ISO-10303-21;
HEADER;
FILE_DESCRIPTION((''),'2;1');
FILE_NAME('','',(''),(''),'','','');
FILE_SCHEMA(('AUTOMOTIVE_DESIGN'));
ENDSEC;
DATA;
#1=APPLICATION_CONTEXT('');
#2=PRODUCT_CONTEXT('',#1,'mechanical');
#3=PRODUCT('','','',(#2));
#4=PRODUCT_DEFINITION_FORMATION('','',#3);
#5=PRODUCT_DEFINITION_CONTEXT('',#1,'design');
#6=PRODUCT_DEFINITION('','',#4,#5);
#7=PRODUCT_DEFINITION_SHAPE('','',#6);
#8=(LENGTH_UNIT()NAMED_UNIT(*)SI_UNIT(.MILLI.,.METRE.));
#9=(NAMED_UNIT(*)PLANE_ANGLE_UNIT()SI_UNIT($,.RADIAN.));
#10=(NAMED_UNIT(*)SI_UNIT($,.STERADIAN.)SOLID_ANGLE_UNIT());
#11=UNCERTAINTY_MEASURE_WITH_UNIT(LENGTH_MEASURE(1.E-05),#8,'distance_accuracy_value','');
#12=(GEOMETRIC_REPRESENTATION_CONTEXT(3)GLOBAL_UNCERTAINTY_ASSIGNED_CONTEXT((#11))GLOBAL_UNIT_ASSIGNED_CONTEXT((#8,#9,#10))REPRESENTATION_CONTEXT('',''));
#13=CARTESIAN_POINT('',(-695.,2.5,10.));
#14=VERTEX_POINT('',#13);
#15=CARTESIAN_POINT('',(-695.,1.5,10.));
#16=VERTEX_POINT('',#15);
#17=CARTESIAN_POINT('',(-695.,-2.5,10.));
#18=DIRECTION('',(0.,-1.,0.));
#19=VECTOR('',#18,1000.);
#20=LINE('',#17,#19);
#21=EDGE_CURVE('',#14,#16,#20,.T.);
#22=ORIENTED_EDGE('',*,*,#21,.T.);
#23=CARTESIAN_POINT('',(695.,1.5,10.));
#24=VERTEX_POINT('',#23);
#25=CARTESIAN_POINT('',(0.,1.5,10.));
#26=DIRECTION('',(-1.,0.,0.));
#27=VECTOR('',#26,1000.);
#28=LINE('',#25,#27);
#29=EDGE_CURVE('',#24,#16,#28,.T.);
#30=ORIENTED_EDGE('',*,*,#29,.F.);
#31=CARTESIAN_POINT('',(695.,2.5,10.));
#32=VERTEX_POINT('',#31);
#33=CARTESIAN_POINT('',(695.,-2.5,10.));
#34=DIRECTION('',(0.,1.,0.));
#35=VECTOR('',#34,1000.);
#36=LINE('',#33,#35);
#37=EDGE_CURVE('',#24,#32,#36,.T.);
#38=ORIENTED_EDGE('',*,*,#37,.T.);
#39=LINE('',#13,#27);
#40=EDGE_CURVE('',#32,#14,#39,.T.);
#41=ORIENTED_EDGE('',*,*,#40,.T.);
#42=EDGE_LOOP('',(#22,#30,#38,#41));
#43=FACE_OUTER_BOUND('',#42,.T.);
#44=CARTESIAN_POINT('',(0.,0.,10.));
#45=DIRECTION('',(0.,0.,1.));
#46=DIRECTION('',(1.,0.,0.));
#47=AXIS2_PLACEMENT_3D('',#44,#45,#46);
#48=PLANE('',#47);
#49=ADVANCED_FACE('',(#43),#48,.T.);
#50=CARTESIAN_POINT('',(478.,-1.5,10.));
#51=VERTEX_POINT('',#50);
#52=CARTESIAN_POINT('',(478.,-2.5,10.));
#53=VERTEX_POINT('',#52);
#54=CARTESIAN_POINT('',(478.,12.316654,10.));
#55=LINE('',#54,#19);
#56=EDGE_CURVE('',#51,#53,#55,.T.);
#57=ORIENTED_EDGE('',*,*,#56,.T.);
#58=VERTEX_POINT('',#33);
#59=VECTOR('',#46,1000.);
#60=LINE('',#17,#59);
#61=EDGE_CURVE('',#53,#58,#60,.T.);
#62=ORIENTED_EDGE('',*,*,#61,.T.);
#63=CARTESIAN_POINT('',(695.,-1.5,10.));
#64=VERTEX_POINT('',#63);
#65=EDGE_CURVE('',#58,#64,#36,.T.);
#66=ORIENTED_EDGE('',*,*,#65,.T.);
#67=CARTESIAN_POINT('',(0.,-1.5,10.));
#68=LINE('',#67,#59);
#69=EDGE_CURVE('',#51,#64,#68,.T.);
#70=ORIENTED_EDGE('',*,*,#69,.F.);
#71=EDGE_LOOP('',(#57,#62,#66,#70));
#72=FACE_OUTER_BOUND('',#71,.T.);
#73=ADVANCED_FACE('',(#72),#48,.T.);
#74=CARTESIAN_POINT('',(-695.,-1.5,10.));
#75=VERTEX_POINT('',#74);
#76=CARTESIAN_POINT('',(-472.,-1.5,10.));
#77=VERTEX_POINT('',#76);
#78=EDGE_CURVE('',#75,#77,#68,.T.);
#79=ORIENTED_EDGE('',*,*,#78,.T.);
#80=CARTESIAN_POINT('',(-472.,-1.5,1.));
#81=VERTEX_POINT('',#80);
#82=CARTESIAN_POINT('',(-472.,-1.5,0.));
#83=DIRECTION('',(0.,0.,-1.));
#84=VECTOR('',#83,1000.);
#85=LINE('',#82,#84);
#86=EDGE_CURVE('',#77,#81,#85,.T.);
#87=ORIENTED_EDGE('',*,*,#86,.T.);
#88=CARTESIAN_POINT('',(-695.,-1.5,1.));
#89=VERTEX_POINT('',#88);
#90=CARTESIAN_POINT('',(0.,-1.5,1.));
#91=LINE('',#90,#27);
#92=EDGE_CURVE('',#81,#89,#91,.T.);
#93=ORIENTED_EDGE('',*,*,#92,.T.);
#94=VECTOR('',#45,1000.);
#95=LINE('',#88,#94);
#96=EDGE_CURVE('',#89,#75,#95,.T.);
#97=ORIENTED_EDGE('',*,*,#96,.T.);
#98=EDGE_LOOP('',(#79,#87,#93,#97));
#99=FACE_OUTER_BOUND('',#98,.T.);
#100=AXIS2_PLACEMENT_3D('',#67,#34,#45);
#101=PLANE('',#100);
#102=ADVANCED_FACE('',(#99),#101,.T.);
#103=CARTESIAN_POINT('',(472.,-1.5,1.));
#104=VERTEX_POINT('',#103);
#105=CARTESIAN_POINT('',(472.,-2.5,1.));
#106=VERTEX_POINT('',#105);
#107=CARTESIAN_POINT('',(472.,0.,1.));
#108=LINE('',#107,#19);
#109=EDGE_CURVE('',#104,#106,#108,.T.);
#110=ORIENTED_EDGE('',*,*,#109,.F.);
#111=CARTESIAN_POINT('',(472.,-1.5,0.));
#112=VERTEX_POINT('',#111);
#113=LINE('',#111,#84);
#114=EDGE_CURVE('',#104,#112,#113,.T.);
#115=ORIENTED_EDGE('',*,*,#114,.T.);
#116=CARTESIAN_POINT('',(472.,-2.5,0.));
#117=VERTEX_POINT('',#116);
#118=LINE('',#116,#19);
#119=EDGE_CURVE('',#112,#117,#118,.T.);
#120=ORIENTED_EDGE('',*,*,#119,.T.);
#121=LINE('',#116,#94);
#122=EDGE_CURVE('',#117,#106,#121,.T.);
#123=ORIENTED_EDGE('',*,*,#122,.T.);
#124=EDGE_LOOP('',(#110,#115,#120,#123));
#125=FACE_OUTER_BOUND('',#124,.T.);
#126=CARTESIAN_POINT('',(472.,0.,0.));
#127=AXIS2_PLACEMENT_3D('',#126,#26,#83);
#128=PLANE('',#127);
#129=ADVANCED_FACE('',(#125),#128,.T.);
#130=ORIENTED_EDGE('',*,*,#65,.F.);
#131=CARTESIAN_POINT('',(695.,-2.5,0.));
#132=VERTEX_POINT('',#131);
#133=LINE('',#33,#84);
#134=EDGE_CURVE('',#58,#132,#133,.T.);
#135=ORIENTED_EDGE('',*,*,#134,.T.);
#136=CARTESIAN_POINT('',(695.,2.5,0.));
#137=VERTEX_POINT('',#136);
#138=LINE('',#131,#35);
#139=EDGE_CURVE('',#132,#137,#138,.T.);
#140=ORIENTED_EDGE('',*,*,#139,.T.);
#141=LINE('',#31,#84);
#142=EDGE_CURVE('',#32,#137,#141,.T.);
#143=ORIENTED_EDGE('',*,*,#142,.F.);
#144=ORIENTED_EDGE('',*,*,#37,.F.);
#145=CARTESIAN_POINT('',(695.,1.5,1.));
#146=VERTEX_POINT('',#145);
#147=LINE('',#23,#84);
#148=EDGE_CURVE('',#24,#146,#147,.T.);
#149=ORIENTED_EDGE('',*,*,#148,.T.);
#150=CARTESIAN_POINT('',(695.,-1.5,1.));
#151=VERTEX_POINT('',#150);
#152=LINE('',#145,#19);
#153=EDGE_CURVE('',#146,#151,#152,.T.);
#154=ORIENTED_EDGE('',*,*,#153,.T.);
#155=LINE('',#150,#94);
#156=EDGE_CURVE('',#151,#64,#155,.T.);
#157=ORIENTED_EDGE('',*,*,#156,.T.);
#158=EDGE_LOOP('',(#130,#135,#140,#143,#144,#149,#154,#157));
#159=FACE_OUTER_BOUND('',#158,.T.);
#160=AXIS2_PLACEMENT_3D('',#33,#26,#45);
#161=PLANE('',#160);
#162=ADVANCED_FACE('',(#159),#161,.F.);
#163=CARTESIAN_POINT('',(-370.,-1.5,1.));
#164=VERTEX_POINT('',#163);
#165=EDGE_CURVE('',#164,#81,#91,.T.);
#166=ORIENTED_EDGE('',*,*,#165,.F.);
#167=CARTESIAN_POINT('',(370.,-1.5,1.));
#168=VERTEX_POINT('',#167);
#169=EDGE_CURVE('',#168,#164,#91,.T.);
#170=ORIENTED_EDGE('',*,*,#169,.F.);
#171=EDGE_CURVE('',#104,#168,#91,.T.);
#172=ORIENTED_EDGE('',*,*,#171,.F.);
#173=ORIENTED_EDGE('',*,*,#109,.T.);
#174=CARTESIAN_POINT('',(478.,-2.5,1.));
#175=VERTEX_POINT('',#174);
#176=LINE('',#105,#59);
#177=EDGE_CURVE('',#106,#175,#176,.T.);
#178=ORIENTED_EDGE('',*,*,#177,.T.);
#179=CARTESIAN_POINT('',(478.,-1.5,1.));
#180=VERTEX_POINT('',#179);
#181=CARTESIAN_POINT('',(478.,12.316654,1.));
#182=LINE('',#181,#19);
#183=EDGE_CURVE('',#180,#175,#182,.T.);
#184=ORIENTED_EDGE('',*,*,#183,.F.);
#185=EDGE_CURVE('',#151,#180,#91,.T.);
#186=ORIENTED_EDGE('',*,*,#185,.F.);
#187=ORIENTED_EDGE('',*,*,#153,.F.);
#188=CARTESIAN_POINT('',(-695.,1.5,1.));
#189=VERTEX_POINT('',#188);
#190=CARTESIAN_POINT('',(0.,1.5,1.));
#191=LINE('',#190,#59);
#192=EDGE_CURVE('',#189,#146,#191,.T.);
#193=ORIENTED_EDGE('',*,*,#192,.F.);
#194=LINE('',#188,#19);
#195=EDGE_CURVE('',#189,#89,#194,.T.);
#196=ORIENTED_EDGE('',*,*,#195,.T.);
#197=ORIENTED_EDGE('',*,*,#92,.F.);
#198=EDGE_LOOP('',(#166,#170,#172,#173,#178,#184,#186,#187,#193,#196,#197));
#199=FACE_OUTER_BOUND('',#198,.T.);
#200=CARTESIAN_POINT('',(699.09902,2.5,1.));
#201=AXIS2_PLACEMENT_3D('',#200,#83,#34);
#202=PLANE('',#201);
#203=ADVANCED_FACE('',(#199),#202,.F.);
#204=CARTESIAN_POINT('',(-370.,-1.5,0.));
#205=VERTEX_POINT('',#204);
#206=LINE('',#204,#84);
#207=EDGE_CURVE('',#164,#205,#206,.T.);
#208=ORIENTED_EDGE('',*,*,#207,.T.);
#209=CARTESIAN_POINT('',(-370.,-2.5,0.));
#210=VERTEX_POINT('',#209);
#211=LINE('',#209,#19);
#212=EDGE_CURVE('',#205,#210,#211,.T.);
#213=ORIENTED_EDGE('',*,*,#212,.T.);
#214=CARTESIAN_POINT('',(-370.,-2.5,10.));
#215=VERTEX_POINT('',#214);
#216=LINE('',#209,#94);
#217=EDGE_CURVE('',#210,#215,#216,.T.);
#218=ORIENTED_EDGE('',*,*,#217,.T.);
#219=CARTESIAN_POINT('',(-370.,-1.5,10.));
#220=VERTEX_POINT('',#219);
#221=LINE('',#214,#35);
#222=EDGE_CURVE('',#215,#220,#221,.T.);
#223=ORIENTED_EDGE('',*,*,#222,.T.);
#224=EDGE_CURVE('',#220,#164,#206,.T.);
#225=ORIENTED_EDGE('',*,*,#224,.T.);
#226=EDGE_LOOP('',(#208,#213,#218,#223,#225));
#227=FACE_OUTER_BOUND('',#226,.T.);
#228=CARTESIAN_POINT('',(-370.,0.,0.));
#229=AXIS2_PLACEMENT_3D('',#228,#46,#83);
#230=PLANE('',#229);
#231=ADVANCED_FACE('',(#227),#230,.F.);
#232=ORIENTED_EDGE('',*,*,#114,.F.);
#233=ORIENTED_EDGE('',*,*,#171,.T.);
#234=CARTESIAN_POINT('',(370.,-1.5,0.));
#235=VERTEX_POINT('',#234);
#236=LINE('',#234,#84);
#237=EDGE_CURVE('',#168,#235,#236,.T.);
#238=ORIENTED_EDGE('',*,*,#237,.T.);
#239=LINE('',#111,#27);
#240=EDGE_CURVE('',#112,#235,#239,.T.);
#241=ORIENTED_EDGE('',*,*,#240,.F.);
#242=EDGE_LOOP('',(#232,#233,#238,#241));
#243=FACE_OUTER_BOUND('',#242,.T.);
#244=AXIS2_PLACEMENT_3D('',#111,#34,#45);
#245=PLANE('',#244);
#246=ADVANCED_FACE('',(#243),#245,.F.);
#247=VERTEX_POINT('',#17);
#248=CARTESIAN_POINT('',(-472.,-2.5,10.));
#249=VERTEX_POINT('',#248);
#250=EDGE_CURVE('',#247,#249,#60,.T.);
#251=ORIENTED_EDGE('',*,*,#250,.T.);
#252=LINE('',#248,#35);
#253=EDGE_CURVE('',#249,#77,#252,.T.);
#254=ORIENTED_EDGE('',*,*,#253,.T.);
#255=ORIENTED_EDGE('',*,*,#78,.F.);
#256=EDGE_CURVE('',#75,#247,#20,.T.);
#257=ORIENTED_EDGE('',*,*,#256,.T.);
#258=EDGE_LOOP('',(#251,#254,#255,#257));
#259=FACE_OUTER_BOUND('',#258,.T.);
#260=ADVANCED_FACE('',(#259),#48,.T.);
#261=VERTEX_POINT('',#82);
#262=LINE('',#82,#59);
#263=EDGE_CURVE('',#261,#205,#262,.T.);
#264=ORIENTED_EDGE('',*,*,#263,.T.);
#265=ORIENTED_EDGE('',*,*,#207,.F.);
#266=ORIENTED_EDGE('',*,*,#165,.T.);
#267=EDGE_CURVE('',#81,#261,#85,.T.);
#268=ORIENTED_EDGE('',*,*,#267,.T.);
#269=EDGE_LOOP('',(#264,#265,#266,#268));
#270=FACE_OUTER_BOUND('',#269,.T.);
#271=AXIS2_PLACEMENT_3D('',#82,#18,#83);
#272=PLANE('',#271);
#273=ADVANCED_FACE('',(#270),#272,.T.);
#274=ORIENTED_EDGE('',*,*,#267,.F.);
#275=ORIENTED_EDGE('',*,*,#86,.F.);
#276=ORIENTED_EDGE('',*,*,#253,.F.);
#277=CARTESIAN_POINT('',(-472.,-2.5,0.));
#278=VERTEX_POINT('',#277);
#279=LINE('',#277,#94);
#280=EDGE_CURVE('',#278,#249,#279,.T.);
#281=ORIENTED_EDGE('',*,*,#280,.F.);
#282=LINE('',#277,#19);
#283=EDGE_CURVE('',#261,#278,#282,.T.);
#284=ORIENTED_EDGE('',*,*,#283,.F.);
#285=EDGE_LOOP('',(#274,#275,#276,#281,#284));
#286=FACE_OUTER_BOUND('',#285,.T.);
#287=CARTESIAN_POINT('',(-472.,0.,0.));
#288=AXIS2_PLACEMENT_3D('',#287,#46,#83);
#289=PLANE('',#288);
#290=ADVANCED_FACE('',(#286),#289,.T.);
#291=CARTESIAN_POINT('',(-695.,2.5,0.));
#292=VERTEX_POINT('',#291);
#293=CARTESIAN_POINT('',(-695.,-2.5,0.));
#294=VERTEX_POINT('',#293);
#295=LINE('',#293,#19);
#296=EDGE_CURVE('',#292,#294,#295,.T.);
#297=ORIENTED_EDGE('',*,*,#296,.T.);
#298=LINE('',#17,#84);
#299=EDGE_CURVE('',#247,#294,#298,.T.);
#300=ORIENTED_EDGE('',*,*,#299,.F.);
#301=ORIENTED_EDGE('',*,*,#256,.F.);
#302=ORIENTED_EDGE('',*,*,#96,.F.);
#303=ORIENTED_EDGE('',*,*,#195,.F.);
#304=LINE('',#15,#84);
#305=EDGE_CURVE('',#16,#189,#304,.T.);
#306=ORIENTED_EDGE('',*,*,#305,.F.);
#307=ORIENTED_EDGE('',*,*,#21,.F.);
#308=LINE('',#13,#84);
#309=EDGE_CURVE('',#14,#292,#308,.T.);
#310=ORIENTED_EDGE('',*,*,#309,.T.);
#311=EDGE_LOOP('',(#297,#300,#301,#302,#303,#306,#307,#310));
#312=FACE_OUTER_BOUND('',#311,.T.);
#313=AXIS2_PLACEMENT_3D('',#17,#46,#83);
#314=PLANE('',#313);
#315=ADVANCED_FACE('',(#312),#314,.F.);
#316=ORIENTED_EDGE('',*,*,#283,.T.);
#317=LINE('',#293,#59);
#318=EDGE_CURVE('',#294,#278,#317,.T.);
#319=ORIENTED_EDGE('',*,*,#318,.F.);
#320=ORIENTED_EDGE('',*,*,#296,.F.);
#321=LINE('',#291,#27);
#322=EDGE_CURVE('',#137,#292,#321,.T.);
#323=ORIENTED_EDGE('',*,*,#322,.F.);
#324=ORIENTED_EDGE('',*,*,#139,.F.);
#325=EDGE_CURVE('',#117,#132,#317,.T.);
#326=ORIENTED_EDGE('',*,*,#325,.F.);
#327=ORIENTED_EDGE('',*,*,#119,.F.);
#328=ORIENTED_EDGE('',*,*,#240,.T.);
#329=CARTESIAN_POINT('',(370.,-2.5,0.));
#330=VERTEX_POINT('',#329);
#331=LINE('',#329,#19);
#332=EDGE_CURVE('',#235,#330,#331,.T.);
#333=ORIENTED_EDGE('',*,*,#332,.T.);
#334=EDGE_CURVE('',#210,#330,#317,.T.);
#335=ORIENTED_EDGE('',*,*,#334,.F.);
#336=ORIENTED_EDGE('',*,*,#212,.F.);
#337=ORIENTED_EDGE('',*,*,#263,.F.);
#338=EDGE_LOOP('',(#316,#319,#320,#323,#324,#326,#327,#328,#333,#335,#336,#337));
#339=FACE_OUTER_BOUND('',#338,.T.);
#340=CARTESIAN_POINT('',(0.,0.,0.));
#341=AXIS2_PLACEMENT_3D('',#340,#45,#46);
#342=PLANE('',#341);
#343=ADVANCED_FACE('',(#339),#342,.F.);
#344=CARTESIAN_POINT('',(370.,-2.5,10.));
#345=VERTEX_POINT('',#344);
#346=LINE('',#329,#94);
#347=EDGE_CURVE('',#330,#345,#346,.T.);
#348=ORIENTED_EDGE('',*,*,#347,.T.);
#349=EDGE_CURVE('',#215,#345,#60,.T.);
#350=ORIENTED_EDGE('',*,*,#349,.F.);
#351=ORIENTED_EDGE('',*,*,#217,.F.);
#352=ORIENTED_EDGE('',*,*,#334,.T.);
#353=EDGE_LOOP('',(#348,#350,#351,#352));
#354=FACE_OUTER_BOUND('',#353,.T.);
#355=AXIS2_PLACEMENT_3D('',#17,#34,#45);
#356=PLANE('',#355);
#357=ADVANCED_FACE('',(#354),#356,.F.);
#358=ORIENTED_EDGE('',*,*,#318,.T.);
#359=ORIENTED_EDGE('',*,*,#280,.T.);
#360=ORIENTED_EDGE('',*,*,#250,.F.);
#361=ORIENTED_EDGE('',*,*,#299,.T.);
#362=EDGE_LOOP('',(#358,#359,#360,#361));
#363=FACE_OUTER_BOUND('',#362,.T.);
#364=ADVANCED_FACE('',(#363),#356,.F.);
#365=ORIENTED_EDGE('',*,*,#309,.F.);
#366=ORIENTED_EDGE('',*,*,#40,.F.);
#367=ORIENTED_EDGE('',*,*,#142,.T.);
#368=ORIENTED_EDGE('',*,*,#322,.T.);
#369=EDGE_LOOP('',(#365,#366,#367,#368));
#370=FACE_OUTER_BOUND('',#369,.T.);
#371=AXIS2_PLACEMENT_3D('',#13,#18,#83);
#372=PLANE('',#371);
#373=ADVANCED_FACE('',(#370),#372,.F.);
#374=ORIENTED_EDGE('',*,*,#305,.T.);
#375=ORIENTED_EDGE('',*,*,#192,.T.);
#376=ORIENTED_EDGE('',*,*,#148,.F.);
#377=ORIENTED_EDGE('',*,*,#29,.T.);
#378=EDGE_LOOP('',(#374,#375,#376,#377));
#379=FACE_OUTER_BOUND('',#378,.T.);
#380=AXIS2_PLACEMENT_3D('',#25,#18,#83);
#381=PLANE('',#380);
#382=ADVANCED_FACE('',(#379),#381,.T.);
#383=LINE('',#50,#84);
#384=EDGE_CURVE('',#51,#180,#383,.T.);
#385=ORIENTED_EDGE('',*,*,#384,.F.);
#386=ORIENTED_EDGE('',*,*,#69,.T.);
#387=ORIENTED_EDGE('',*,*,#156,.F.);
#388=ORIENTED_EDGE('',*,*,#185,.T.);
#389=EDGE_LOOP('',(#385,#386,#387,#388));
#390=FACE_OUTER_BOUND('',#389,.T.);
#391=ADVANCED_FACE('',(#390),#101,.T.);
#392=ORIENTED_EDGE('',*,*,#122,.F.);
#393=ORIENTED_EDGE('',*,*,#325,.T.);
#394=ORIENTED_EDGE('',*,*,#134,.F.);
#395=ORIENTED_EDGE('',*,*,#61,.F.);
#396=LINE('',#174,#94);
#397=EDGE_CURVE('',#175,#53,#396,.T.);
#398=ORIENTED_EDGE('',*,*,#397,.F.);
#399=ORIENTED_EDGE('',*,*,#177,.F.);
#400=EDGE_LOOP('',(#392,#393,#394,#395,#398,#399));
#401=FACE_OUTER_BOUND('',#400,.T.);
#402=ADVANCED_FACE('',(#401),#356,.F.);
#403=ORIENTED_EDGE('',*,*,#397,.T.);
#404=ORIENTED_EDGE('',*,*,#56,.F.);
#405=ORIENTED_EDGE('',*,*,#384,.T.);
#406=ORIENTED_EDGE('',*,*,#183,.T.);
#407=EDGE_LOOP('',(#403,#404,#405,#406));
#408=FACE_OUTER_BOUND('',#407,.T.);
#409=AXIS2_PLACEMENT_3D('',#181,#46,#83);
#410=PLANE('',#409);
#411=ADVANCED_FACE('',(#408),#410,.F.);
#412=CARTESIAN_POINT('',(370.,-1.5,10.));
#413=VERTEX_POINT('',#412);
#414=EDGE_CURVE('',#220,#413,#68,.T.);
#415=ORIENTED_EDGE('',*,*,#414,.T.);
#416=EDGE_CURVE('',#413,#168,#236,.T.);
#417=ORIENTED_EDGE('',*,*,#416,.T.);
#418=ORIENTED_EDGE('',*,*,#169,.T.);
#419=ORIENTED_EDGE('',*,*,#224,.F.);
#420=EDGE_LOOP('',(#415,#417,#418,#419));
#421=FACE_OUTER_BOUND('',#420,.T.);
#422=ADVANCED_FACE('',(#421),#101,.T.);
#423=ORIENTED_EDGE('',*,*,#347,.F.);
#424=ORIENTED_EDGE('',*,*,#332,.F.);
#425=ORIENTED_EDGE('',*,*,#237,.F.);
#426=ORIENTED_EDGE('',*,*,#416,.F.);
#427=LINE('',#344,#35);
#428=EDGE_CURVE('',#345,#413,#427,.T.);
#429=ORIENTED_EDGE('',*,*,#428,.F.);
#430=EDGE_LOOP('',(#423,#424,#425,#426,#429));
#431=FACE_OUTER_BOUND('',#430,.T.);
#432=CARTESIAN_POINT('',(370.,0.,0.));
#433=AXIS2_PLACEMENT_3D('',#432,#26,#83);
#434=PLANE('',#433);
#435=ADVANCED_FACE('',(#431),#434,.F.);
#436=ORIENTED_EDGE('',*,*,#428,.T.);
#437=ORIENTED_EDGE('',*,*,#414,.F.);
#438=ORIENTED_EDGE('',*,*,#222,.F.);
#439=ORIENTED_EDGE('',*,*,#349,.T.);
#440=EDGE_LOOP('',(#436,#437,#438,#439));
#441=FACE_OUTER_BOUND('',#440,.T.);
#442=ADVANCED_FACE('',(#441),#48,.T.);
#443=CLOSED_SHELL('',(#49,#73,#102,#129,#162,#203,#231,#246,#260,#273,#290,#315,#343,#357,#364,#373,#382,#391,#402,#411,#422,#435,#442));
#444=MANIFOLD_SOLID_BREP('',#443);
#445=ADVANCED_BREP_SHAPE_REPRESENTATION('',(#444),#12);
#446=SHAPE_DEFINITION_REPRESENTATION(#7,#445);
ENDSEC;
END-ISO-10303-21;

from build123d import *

# Parameters (mm, degrees)
SKETCH_1_W               = 1390
SKETCH_1_H               = 5
SKETCH_1_W_2             = 1388
SKETCH_1_H_2             = 3
EXTRUDE_1_DEPTH          = 10
SKETCH_2_W               = 1
SKETCH_2_H               = 5
EXTRUDE_1_2_DEPTH        = 1389
CUT_EXTRUDE_1_DEPTH      = 1390.038246414
CUT_EXTRUDE_1_DEPTH_BACK = 1390.038246414
SKETCH_3_W               = 9
SKETCH_3_H               = 3
CUT_EXTRUDE_START        = -325
SKETCH_4_W               = 10
SKETCH_4_H               = 1
CUT_EXTRUDE_2_DEPTH      = 102
SKETCH_5_W               = 6
SKETCH_5_H               = 9
CUT_EXTRUDE_5_DEPTH      = 4


with BuildPart() as part:
    # 草图1 → Extrude 1 (new body)
    with BuildSketch(Plane.XY):
        Rectangle(SKETCH_1_W, SKETCH_1_H)
        Rectangle(SKETCH_1_W_2, SKETCH_1_H_2, mode=Mode.SUBTRACT)
    extrude(amount=EXTRUDE_1_DEPTH)

    # 草图2 → Extrude 1 2 (add)
    with BuildSketch(Plane.ZY.offset(695)):
        with Locations((0.5, 0)):
            Rectangle(SKETCH_2_W, SKETCH_2_H)
    extrude(amount=-EXTRUDE_1_2_DEPTH)

    # 草图3 → 切除-拉伸1 (cut, two sides: drawn at the far end of the back side and taken through both)
    with BuildSketch(Plane.ZY.offset(-694).offset(-CUT_EXTRUDE_1_DEPTH_BACK)):
        with Locations((5.5, 0)):
            Rectangle(SKETCH_3_W, SKETCH_3_H)
    extrude(amount=CUT_EXTRUDE_1_DEPTH + CUT_EXTRUDE_1_DEPTH_BACK, mode=Mode.SUBTRACT)

    # 草图4 → 切除-拉伸2 (cut)
    with BuildSketch(Plane.ZY.offset(695).offset(CUT_EXTRUDE_START)):
        with Locations((5, -2)):
            Rectangle(SKETCH_4_W, SKETCH_4_H)
    cut_extrude_2 = extrude(amount=CUT_EXTRUDE_2_DEPTH, mode=Mode.SUBTRACT)

    # 镜向1: 切除-拉伸2 across plane
    add(cut_extrude_2.mirror(Plane(origin=(0, 0, 0), x_dir=(0, 0, 1), z_dir=(1, 0, 0))), mode=Mode.SUBTRACT)

    # 草图5 → 切除-拉伸5 (cut)
    with BuildSketch(Plane.XZ.offset(2.5)):
        with Locations((475, 5.5)):
            Rectangle(SKETCH_5_W, SKETCH_5_H)
    extrude(amount=-CUT_EXTRUDE_5_DEPTH, mode=Mode.SUBTRACT)


solid = part.part
